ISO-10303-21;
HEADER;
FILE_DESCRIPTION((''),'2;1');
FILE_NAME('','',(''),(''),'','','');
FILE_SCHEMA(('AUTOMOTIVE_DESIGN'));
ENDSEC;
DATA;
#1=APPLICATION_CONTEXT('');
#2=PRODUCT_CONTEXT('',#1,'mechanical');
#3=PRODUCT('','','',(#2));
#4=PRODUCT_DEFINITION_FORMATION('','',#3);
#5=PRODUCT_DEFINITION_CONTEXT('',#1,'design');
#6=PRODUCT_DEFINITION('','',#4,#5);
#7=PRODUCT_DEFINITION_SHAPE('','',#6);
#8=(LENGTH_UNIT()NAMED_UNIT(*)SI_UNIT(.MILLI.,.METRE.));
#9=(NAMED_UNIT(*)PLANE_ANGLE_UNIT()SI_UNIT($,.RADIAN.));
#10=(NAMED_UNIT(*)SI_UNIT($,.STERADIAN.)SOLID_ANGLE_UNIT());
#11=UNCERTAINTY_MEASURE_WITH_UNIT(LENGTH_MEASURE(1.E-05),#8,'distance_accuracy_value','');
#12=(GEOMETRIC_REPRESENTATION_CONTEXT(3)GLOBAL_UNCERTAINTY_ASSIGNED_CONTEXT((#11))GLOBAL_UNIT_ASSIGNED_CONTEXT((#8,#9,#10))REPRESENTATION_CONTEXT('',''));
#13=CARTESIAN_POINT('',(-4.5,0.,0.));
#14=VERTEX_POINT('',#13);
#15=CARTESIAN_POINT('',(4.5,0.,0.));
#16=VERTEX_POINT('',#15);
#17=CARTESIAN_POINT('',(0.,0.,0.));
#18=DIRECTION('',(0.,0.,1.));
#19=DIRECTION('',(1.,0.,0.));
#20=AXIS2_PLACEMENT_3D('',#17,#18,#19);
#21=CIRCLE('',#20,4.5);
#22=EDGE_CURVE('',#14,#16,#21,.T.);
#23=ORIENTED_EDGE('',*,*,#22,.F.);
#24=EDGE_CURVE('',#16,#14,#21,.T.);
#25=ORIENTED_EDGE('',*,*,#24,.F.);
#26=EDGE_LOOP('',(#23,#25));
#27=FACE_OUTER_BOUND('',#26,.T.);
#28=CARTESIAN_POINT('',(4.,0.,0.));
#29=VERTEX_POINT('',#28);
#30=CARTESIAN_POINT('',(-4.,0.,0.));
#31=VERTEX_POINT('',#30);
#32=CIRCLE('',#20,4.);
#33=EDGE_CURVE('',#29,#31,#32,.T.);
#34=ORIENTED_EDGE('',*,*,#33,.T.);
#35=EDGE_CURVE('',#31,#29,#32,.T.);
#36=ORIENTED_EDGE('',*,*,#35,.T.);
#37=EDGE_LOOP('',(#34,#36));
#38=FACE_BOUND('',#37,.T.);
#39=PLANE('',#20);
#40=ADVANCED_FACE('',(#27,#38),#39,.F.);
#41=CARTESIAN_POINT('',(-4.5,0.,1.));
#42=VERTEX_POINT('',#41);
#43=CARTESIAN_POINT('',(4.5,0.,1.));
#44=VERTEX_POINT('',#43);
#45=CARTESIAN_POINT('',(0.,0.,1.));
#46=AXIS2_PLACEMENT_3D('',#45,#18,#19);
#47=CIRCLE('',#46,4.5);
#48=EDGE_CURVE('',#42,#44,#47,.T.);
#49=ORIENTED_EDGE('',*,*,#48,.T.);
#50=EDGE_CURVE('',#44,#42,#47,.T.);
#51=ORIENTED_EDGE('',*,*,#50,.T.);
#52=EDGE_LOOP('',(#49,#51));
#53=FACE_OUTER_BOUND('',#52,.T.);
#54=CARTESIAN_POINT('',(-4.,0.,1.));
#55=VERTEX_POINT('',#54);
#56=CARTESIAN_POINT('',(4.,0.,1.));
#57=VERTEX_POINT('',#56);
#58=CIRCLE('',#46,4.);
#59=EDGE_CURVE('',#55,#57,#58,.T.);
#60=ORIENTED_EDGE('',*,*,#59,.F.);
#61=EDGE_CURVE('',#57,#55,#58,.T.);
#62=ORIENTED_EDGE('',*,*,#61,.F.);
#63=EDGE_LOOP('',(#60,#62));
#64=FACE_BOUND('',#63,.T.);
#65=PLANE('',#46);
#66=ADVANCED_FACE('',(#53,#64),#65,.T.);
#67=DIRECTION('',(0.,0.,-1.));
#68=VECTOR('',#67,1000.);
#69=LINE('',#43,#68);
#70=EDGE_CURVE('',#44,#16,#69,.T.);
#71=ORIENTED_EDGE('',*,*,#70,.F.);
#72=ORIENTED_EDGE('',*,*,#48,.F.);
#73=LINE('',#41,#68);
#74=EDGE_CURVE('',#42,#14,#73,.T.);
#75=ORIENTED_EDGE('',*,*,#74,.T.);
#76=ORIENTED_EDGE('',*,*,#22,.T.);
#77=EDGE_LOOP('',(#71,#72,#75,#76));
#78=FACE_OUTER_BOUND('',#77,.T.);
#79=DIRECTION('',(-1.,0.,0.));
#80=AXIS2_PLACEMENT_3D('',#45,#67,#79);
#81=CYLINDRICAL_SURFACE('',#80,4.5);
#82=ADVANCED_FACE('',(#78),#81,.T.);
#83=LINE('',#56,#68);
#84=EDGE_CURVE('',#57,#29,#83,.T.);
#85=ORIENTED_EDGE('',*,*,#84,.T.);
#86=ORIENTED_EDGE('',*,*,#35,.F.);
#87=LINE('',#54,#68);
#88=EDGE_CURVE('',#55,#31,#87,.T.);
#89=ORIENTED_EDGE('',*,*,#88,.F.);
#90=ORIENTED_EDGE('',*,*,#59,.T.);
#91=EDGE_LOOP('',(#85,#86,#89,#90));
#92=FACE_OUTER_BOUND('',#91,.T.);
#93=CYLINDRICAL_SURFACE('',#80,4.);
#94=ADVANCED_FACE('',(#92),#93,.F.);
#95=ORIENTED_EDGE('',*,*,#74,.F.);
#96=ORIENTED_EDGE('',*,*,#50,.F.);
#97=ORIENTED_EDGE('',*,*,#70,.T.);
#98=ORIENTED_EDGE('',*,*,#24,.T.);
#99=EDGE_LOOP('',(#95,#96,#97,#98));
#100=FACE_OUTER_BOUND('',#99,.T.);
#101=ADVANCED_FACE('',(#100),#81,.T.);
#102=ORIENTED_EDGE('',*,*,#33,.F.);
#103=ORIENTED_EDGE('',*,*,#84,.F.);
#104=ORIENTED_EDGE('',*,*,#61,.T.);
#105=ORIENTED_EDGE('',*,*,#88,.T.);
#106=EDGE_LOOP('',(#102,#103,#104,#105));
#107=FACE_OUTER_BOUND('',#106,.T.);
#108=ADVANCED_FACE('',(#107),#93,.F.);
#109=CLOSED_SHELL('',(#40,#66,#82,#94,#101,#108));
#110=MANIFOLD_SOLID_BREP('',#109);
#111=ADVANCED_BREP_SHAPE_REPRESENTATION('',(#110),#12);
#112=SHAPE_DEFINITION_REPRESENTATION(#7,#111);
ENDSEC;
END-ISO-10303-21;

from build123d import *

# Parameters (mm, degrees)
SKETCH1_R           = 4.5
SKETCH1_R_2         = 4
BOSS_EXTRUDE1_DEPTH = 1


with BuildPart() as part:
    # Sketch1 → Boss-Extrude1 (new body)
    with BuildSketch(Plane.XY):
        Circle(SKETCH1_R)
        Circle(SKETCH1_R_2, mode=Mode.SUBTRACT)
    extrude(amount=BOSS_EXTRUDE1_DEPTH)


solid = part.part
